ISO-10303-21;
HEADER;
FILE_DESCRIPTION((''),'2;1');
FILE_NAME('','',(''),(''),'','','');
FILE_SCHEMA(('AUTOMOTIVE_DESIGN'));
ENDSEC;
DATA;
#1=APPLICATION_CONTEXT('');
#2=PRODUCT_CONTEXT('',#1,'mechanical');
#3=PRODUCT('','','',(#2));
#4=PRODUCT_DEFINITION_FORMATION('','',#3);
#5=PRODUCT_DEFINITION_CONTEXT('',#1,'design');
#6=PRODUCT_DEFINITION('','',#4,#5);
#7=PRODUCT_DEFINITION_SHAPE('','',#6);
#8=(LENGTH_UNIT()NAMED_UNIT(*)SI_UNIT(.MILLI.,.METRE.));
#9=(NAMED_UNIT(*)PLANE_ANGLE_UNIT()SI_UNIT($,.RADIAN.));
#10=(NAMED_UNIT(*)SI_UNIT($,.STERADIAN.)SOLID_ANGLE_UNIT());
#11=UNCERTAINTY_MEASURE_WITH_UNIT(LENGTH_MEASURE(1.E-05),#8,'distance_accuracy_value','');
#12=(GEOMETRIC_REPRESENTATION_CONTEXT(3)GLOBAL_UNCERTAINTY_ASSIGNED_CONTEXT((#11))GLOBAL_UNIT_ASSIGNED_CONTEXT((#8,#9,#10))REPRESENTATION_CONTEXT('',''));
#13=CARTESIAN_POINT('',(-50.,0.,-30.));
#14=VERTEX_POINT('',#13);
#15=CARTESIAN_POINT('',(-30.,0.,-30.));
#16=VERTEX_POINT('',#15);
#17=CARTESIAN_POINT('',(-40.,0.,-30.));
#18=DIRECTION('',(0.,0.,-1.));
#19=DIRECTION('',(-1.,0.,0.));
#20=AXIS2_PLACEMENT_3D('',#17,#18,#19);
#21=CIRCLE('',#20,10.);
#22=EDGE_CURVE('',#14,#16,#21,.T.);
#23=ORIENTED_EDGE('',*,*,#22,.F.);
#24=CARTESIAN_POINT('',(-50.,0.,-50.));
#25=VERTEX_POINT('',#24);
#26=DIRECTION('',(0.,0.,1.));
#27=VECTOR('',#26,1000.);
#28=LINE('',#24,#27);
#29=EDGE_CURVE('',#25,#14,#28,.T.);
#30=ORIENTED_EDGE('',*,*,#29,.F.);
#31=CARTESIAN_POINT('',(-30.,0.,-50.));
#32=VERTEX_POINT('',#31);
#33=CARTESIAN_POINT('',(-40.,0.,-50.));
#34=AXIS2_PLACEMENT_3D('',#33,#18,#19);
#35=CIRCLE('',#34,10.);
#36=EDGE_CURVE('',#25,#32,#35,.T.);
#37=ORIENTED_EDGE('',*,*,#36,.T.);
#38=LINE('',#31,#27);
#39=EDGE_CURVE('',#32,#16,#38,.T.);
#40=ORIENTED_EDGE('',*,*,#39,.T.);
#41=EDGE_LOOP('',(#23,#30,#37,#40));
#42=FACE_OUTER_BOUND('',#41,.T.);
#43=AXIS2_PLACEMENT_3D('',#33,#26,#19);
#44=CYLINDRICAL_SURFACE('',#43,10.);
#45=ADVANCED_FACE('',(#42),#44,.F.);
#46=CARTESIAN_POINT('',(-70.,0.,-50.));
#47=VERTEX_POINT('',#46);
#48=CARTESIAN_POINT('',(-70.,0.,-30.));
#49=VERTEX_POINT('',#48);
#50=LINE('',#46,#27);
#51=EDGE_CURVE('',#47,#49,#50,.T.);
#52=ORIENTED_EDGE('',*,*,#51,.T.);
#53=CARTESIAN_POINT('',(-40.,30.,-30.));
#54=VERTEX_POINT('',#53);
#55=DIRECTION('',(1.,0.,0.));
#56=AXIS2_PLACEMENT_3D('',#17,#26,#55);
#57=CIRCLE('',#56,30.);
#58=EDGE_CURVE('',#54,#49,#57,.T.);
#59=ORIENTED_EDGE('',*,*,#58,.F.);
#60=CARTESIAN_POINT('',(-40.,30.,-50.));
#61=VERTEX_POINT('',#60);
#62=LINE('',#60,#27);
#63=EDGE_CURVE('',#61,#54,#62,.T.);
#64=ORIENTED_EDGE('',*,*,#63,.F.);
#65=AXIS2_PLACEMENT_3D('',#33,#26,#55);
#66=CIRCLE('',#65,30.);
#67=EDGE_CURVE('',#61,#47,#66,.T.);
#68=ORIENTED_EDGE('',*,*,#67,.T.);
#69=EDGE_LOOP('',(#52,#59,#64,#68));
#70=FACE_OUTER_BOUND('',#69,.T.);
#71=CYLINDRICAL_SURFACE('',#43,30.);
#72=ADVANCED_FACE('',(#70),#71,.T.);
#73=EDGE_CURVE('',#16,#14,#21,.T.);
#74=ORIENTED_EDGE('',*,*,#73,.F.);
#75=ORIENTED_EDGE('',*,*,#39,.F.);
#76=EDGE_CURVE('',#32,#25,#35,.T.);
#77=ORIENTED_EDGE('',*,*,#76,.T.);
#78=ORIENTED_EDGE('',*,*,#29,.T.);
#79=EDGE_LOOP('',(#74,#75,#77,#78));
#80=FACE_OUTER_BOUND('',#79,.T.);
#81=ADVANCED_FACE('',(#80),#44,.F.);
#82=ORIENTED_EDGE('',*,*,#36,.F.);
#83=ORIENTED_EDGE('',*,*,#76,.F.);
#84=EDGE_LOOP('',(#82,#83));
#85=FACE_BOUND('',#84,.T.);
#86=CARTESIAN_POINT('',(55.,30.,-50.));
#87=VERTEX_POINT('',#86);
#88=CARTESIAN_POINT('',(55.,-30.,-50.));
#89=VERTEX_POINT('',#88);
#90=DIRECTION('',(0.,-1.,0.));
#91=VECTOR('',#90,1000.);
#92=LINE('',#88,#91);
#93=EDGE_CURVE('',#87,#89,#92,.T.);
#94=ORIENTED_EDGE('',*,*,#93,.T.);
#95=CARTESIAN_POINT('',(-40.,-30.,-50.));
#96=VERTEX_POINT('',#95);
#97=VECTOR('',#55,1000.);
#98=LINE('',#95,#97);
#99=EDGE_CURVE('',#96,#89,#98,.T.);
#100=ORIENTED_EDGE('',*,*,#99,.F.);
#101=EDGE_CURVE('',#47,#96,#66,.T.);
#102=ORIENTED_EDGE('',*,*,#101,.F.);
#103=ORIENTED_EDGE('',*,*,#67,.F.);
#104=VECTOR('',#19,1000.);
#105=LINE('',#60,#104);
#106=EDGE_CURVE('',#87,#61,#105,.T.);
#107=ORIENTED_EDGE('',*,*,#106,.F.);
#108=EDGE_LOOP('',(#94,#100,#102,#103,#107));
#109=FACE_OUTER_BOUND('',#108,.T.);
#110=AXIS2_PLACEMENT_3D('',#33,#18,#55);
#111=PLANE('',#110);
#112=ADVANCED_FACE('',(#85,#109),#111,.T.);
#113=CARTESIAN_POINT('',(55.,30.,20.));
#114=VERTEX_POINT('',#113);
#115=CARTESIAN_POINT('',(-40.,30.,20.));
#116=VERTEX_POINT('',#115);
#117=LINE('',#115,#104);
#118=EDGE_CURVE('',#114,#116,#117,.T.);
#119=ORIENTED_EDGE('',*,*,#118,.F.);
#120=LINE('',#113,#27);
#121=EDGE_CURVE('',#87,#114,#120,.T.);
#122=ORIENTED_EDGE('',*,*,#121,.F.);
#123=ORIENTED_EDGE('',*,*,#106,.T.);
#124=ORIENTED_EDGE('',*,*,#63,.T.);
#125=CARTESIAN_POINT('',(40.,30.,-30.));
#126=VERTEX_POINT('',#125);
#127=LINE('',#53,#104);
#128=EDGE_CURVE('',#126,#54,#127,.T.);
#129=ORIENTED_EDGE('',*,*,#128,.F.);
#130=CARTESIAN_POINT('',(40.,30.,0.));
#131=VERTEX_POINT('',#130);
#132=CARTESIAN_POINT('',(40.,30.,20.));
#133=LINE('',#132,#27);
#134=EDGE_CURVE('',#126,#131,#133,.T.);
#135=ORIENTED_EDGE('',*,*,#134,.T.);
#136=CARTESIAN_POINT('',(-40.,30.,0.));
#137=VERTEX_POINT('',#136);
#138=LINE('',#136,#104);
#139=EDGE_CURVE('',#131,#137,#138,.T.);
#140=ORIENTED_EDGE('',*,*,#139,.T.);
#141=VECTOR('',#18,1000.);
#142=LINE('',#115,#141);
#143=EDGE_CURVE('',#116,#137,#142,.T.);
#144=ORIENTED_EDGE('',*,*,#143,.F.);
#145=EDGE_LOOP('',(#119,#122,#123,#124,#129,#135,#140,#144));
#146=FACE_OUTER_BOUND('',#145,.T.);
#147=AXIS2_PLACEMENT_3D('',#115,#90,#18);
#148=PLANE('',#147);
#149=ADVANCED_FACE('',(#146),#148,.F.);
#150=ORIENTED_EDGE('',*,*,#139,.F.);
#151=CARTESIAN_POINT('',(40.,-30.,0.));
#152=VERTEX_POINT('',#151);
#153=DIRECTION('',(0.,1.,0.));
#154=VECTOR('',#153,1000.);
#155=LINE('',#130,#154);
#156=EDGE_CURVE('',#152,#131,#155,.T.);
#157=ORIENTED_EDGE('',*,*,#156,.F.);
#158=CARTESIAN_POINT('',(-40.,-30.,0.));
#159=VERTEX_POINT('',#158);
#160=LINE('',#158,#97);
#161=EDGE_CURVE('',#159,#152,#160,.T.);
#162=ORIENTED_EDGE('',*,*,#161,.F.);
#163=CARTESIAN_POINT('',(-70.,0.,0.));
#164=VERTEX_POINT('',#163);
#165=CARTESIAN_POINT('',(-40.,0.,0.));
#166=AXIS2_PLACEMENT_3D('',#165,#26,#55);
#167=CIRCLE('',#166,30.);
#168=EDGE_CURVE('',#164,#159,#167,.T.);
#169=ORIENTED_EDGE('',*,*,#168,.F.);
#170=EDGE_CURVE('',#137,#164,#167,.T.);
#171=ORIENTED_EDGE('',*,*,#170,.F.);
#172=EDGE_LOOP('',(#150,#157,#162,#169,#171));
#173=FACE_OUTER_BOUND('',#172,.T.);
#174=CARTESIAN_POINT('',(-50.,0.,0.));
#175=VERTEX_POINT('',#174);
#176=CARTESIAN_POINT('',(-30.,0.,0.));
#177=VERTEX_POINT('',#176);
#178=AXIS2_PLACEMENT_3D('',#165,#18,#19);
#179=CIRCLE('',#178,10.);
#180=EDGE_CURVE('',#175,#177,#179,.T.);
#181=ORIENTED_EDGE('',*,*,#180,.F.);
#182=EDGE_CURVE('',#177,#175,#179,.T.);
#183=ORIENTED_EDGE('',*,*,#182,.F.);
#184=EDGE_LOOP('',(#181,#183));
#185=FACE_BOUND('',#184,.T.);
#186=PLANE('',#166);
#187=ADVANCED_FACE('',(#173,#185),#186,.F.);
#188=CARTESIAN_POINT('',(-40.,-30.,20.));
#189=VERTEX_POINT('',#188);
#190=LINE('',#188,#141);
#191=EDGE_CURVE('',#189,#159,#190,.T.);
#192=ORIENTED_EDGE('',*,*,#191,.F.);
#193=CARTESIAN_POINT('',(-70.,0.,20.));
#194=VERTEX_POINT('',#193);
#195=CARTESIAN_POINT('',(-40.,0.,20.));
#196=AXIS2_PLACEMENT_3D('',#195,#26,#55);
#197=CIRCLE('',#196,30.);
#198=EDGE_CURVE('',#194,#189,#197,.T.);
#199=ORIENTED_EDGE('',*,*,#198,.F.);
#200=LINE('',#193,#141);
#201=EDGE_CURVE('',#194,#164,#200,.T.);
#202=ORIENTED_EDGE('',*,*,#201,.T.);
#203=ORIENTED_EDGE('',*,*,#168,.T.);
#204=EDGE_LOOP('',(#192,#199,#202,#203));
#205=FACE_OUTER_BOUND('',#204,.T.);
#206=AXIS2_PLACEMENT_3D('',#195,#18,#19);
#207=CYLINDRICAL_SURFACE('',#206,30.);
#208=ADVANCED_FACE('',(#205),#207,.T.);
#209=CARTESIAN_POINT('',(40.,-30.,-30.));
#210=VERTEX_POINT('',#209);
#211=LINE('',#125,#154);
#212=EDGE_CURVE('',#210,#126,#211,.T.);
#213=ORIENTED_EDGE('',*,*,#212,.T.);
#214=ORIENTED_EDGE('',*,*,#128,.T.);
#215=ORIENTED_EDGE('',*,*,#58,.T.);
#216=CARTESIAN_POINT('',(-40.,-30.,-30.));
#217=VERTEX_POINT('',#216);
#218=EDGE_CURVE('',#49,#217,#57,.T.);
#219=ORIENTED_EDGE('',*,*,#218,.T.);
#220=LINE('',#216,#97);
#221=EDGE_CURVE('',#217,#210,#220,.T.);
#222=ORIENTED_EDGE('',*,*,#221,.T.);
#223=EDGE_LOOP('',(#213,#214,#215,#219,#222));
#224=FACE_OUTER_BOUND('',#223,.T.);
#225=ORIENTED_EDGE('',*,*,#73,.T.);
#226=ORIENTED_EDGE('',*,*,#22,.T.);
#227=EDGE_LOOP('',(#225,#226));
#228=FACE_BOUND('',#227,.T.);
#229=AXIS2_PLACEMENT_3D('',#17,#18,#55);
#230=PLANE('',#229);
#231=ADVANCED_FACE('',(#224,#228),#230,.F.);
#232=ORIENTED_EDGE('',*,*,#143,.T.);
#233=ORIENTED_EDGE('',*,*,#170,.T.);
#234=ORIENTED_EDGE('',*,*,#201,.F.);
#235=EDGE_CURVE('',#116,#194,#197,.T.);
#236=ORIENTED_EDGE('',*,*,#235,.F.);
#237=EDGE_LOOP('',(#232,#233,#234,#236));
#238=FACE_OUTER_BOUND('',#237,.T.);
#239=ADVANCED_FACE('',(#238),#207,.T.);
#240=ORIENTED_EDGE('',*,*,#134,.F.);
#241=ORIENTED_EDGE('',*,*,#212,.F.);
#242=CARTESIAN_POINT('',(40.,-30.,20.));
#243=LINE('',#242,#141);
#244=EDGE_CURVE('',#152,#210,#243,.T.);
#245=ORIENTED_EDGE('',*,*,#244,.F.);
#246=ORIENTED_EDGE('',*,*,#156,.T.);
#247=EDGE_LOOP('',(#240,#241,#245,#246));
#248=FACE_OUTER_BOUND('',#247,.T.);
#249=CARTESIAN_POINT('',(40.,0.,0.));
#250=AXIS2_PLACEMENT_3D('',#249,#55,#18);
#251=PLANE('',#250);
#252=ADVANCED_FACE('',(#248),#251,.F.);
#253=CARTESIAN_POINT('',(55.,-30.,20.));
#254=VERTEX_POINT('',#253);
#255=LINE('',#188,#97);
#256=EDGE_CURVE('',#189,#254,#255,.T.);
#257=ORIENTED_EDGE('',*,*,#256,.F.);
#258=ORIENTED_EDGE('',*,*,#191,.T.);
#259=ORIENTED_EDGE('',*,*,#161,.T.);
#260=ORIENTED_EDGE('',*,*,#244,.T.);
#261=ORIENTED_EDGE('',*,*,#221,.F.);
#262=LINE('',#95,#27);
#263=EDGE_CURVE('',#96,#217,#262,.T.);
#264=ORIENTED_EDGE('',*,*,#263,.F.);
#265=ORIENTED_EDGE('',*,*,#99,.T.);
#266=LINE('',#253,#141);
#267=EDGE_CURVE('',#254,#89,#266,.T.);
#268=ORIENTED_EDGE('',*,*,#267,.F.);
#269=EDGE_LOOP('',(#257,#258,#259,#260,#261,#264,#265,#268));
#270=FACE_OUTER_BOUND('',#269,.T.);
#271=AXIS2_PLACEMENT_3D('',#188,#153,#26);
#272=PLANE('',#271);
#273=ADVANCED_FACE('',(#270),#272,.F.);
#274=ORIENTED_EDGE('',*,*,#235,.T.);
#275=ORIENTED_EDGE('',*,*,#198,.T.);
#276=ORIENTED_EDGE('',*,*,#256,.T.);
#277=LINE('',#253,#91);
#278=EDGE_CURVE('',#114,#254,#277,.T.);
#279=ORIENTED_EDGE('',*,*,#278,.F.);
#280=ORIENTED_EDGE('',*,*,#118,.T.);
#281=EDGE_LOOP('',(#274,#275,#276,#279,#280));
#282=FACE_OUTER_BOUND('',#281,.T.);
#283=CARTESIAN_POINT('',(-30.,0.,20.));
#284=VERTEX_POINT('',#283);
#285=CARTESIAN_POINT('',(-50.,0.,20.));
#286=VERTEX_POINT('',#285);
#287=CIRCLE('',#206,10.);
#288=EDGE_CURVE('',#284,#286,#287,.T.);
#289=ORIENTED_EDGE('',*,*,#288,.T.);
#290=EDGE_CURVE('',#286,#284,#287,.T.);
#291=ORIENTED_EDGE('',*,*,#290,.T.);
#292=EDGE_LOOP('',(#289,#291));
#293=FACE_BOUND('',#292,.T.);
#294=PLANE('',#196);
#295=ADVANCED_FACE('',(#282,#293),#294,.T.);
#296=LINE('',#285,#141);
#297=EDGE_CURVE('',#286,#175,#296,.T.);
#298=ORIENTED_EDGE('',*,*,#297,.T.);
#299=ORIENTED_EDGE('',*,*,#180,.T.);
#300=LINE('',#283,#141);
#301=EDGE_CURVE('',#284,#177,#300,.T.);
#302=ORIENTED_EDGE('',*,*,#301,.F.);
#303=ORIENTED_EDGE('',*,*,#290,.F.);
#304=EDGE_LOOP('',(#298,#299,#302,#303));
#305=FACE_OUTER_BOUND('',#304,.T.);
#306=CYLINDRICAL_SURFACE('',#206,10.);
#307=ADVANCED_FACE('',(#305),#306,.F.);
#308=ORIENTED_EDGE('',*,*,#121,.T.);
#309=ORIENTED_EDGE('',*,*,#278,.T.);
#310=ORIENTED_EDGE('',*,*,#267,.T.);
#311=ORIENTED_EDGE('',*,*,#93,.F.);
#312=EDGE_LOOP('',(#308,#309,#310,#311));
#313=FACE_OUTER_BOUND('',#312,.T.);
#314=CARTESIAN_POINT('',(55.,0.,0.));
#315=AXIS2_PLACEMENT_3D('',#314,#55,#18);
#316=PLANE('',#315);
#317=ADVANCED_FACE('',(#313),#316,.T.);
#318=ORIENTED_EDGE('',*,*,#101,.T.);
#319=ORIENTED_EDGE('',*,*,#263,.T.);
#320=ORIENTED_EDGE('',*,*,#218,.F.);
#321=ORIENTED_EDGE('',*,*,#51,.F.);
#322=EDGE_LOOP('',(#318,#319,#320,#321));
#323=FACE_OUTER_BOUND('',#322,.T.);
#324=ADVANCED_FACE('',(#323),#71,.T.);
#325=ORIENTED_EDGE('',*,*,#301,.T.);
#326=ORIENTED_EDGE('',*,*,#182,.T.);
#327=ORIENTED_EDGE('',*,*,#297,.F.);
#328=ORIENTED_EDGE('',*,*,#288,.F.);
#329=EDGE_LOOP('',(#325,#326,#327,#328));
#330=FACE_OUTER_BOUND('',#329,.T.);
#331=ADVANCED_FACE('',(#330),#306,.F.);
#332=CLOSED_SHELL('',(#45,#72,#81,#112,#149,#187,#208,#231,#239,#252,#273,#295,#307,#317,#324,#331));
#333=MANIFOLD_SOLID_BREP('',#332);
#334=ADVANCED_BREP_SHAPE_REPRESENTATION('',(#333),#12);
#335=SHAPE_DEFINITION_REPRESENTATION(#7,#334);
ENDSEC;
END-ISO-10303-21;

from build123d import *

# Parameters (mm, degrees)
BOSS_EXTRUDE1_DEPTH = 20
SKETCH2_R           = 10
CUT_EXTRUDE1_DEPTH  = 79.74007874
SKETCH3_W           = 35
SKETCH3_H           = 60
BOSS_EXTRUDE5_DEPTH = 15


with BuildPart() as part:
    # Sketch1 → Boss-Extrude1 (new body)
    with BuildSketch(Plane.XY):
        with BuildLine():
            Line((-40, 30), (40, 30))
            Line((40, 30), (40, -30))
            Line((40, -30), (-40, -30))
            ThreePointArc((-40, -30), (-70, 0), (-40, 30))
        make_face()
    extrude(amount=BOSS_EXTRUDE1_DEPTH)

    # Sketch2 → Cut-Extrude1 (cut, through all)
    with BuildSketch(Plane(origin=(0, 0, 0), x_dir=(-1, 0, 0), z_dir=(0, 0, -1))):
        with Locations((40, 0)):
            Circle(SKETCH2_R)
    extrude(amount=-CUT_EXTRUDE1_DEPTH, mode=Mode.SUBTRACT)

    # Sketch3 → Boss-Extrude5 (add)
    with BuildSketch(Plane(origin=(40, 0, 0), x_dir=(0, 0, -1), z_dir=(1, 0, 0))):
        with Locations((-2.5, 0)):
            Rectangle(SKETCH3_W, SKETCH3_H)
    extrude(amount=BOSS_EXTRUDE5_DEPTH)

    # Mirror1: part across plane


with BuildPart() as part_1:
    add(part.part)
    add(part.part.mirror(Plane(origin=(55, -30, -15), x_dir=(1, 0, 0), z_dir=(0, 0, 1))))


solid = part_1.part
